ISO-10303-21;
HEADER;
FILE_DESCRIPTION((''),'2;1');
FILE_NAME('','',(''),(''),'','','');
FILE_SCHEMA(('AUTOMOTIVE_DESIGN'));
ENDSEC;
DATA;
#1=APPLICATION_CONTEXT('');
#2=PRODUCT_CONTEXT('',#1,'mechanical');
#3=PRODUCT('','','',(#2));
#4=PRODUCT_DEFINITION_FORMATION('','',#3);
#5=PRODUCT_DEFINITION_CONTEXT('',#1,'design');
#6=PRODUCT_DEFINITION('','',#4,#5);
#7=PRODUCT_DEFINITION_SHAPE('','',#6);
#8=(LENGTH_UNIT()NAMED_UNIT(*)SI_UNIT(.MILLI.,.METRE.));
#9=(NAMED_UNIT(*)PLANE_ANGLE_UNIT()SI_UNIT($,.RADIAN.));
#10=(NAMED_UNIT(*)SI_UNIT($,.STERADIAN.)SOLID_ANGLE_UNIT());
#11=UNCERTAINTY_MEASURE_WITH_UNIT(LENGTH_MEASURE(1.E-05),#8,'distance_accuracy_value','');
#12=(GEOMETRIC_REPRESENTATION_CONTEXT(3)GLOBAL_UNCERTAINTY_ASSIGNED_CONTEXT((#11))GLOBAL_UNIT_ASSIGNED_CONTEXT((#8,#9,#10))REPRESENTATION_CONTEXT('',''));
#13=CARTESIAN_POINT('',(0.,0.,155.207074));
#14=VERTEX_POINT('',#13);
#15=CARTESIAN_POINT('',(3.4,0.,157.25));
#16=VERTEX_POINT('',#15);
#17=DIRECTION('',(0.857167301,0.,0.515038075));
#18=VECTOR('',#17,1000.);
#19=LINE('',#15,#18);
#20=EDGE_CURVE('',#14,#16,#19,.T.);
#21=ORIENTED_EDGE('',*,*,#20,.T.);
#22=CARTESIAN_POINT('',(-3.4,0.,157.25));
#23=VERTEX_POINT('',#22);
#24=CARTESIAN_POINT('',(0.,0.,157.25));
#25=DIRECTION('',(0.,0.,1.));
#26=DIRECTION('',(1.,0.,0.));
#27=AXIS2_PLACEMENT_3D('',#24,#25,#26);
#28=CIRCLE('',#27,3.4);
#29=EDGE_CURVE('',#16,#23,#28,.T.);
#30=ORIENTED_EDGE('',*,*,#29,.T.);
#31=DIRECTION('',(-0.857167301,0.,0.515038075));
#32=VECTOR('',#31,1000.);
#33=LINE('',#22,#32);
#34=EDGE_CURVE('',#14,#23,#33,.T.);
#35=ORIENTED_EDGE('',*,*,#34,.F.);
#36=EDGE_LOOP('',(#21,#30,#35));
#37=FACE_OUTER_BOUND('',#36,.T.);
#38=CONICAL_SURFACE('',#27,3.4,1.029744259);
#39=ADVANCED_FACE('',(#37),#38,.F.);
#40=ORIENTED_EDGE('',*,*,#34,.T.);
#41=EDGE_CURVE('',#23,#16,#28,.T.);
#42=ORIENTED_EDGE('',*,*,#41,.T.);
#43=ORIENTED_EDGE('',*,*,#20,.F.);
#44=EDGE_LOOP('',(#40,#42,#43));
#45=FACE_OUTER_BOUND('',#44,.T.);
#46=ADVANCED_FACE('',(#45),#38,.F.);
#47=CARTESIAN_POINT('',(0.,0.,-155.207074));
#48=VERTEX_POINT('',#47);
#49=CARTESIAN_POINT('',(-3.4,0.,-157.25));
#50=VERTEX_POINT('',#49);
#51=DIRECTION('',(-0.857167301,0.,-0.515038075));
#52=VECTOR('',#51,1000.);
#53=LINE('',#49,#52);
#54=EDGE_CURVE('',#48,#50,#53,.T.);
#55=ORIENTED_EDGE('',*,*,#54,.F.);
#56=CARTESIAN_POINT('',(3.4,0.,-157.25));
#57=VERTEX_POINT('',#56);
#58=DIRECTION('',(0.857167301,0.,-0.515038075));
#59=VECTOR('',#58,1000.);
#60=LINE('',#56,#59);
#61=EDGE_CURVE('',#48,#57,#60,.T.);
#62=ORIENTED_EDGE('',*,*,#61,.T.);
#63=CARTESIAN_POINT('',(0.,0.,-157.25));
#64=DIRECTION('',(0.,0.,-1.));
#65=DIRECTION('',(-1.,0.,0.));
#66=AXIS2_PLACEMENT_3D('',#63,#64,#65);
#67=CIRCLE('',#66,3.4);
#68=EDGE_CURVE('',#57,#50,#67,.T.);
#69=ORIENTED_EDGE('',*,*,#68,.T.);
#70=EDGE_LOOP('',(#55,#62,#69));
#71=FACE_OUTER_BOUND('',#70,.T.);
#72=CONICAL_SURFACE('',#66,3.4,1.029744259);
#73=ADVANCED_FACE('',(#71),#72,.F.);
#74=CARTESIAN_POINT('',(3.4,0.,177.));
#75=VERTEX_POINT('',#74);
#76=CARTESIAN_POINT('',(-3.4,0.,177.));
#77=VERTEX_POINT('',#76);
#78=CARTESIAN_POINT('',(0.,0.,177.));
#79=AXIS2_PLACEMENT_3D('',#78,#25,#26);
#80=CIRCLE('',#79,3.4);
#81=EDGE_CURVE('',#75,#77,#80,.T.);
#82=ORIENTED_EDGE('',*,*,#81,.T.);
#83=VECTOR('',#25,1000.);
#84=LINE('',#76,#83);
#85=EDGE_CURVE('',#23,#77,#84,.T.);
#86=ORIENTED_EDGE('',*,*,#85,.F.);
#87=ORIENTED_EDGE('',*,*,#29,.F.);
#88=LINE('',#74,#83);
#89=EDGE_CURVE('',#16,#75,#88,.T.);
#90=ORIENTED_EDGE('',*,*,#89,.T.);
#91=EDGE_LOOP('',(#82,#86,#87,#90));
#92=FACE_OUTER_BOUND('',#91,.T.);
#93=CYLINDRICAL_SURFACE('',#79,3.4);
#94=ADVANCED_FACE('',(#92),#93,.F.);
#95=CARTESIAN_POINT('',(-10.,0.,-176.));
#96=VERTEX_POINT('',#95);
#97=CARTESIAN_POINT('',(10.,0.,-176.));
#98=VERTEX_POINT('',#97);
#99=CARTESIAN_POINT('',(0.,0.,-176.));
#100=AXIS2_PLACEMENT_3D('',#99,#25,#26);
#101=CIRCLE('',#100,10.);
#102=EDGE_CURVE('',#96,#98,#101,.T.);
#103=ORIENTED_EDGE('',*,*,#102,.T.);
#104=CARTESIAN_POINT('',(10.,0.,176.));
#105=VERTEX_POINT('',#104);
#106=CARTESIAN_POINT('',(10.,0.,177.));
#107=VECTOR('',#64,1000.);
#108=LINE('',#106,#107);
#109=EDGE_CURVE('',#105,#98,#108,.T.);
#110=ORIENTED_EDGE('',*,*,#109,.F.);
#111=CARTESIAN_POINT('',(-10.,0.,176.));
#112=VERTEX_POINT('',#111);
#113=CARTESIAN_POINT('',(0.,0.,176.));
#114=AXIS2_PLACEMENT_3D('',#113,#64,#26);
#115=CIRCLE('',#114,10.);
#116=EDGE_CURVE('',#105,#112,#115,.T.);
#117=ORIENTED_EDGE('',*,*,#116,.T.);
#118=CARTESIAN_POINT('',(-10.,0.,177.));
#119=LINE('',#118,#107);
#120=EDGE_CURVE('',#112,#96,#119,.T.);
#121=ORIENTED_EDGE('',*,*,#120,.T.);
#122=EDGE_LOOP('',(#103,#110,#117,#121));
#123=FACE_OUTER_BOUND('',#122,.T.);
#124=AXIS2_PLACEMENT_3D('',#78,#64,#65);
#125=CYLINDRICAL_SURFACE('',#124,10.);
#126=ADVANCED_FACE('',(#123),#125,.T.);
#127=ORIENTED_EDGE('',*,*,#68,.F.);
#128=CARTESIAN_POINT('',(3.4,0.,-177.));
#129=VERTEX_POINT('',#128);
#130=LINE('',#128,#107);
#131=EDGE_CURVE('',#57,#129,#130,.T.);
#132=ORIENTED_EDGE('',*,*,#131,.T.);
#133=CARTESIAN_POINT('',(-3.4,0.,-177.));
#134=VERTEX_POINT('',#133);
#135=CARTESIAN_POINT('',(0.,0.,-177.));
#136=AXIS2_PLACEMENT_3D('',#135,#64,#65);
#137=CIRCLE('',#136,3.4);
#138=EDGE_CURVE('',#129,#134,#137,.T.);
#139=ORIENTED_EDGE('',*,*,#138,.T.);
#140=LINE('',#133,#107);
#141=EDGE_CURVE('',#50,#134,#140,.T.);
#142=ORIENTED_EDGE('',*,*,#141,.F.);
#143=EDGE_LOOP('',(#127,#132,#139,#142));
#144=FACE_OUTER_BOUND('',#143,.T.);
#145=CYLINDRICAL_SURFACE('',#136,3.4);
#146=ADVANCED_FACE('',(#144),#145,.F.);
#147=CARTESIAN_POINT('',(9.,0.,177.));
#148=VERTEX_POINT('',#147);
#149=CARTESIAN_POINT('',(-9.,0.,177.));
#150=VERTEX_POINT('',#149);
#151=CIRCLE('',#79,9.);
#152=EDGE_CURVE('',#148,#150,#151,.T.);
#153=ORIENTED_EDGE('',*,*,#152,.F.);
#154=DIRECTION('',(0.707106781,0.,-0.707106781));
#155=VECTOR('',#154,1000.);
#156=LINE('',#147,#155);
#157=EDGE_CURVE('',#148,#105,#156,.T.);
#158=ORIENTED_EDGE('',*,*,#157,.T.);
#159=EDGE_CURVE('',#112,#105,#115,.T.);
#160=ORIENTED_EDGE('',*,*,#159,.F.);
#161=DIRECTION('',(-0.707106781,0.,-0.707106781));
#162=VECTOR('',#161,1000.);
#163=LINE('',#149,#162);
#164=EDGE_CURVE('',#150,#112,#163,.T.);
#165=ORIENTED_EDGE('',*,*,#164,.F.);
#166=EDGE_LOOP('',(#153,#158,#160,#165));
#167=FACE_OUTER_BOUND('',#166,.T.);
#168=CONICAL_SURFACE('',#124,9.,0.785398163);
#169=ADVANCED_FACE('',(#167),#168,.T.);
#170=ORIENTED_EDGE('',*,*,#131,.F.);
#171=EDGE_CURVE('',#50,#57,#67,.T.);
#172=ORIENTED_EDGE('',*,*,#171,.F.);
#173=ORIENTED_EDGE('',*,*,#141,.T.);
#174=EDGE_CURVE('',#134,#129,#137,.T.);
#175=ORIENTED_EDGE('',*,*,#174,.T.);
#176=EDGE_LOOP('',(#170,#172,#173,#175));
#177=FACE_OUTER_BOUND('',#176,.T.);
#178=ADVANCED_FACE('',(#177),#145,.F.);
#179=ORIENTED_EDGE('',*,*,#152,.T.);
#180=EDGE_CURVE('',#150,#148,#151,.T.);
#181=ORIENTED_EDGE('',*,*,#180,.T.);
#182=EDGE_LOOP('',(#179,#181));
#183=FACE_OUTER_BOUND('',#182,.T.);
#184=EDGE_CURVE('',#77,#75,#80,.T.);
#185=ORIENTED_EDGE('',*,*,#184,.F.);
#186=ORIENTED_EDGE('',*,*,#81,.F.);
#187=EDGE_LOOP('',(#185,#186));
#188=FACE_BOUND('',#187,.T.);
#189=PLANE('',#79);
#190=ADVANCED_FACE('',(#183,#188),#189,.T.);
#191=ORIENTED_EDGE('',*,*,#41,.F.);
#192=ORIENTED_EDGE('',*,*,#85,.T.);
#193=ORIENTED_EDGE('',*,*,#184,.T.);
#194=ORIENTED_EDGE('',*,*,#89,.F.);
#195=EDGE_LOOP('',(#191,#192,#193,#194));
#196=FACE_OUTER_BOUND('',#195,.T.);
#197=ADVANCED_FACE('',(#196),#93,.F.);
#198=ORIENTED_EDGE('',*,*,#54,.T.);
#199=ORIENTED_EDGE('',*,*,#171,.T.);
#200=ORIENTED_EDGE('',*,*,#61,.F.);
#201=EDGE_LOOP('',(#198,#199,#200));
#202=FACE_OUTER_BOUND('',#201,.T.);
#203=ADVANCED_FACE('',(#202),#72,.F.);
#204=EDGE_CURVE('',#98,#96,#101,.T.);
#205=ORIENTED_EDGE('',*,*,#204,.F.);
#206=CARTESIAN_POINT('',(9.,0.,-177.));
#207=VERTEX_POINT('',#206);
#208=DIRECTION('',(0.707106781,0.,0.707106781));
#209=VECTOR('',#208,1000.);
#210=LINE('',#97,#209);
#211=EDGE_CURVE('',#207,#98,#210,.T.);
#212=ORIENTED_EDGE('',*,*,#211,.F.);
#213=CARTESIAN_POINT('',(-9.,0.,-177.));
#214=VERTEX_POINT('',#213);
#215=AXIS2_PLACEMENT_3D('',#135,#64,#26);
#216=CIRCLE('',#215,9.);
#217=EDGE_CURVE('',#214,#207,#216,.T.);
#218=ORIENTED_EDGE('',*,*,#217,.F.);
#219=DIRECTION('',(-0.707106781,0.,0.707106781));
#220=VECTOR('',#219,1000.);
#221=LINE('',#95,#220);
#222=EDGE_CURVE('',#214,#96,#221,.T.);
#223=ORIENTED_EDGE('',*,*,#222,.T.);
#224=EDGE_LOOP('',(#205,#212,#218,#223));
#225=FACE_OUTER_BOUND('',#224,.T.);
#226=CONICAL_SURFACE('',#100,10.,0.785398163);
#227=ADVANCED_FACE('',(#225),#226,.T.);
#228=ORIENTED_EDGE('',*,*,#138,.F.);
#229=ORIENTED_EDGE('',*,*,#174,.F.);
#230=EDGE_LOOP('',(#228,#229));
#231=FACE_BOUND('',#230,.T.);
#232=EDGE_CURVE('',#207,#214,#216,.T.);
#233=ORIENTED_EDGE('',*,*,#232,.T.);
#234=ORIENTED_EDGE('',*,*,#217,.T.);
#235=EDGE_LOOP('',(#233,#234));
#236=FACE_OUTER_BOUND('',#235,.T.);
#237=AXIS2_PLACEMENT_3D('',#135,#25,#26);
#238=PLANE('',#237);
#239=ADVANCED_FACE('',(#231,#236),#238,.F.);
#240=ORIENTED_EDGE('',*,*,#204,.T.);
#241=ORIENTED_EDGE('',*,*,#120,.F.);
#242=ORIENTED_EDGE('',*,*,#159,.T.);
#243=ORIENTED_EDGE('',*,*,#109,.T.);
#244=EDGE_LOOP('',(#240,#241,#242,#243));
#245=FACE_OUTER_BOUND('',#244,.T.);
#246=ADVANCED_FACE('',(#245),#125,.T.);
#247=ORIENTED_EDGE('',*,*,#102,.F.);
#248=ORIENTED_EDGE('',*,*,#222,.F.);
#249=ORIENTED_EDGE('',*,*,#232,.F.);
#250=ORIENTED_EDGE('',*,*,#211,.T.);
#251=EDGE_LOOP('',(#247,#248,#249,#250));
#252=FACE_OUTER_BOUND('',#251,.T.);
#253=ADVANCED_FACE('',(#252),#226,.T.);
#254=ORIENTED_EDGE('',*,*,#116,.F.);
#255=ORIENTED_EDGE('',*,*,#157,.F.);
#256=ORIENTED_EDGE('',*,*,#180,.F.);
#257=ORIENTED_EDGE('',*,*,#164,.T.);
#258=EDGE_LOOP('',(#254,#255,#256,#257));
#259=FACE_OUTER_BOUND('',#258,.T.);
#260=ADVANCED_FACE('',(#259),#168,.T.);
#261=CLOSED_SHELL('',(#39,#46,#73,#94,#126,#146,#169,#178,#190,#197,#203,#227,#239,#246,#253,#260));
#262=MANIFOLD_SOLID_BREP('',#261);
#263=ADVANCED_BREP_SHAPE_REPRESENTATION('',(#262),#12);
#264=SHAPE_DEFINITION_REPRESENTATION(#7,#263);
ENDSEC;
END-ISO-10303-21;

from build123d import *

# Parameters (mm, degrees)
SKETCH_1_R             = 10
EXTRUDE_1_DEPTH        = 177
HOLE_WIZARD_M8_1_D     = 6.8
HOLE_WIZARD_M8_1_DEPTH = 19.75
HOLE_WIZARD_M8_1_TIP   = 2.042926105
HOLE_WIZARD_M8_2_D     = 6.8
HOLE_WIZARD_M8_2_DEPTH = 19.75
HOLE_WIZARD_M8_2_TIP   = 2.042926105
CHAMFER_1_SIZE         = 1


with BuildPart() as part:
    # 草图1 → 凸台-拉伸1 (new, symmetric)
    with BuildSketch(Plane.XY):
        Circle(SKETCH_1_R)
    extrude(amount=EXTRUDE_1_DEPTH, both=True)

    # M8 螺纹孔1
    with Locations(Plane(origin=(0, 0, -177), x_dir=(-1, 0, 0), z_dir=(0, 0, -1))):
        with Locations((0, 0)):
            Hole(HOLE_WIZARD_M8_1_D / 2, depth=HOLE_WIZARD_M8_1_DEPTH)
            with Locations((0, 0, -(HOLE_WIZARD_M8_1_DEPTH + HOLE_WIZARD_M8_1_TIP / 2))):  # 118° drill point
                Cone(0, HOLE_WIZARD_M8_1_D / 2, HOLE_WIZARD_M8_1_TIP, mode=Mode.SUBTRACT)

    # M8 螺纹孔2
    with Locations(Plane.XY.offset(177)):
        with Locations((0, 0)):
            Hole(HOLE_WIZARD_M8_2_D / 2, depth=HOLE_WIZARD_M8_2_DEPTH)
            with Locations((0, 0, -(HOLE_WIZARD_M8_2_DEPTH + HOLE_WIZARD_M8_2_TIP / 2))):  # 118° drill point
                Cone(0, HOLE_WIZARD_M8_2_D / 2, HOLE_WIZARD_M8_2_TIP, mode=Mode.SUBTRACT)

    # 倒角1
    chamfer_1_edges = [part.edges().sort_by_distance(p)[0] for p in [
        (-10, 0, -177),
        (-10, 0, 177),
    ]]
    chamfer(chamfer_1_edges, length=CHAMFER_1_SIZE)


solid = part.part
